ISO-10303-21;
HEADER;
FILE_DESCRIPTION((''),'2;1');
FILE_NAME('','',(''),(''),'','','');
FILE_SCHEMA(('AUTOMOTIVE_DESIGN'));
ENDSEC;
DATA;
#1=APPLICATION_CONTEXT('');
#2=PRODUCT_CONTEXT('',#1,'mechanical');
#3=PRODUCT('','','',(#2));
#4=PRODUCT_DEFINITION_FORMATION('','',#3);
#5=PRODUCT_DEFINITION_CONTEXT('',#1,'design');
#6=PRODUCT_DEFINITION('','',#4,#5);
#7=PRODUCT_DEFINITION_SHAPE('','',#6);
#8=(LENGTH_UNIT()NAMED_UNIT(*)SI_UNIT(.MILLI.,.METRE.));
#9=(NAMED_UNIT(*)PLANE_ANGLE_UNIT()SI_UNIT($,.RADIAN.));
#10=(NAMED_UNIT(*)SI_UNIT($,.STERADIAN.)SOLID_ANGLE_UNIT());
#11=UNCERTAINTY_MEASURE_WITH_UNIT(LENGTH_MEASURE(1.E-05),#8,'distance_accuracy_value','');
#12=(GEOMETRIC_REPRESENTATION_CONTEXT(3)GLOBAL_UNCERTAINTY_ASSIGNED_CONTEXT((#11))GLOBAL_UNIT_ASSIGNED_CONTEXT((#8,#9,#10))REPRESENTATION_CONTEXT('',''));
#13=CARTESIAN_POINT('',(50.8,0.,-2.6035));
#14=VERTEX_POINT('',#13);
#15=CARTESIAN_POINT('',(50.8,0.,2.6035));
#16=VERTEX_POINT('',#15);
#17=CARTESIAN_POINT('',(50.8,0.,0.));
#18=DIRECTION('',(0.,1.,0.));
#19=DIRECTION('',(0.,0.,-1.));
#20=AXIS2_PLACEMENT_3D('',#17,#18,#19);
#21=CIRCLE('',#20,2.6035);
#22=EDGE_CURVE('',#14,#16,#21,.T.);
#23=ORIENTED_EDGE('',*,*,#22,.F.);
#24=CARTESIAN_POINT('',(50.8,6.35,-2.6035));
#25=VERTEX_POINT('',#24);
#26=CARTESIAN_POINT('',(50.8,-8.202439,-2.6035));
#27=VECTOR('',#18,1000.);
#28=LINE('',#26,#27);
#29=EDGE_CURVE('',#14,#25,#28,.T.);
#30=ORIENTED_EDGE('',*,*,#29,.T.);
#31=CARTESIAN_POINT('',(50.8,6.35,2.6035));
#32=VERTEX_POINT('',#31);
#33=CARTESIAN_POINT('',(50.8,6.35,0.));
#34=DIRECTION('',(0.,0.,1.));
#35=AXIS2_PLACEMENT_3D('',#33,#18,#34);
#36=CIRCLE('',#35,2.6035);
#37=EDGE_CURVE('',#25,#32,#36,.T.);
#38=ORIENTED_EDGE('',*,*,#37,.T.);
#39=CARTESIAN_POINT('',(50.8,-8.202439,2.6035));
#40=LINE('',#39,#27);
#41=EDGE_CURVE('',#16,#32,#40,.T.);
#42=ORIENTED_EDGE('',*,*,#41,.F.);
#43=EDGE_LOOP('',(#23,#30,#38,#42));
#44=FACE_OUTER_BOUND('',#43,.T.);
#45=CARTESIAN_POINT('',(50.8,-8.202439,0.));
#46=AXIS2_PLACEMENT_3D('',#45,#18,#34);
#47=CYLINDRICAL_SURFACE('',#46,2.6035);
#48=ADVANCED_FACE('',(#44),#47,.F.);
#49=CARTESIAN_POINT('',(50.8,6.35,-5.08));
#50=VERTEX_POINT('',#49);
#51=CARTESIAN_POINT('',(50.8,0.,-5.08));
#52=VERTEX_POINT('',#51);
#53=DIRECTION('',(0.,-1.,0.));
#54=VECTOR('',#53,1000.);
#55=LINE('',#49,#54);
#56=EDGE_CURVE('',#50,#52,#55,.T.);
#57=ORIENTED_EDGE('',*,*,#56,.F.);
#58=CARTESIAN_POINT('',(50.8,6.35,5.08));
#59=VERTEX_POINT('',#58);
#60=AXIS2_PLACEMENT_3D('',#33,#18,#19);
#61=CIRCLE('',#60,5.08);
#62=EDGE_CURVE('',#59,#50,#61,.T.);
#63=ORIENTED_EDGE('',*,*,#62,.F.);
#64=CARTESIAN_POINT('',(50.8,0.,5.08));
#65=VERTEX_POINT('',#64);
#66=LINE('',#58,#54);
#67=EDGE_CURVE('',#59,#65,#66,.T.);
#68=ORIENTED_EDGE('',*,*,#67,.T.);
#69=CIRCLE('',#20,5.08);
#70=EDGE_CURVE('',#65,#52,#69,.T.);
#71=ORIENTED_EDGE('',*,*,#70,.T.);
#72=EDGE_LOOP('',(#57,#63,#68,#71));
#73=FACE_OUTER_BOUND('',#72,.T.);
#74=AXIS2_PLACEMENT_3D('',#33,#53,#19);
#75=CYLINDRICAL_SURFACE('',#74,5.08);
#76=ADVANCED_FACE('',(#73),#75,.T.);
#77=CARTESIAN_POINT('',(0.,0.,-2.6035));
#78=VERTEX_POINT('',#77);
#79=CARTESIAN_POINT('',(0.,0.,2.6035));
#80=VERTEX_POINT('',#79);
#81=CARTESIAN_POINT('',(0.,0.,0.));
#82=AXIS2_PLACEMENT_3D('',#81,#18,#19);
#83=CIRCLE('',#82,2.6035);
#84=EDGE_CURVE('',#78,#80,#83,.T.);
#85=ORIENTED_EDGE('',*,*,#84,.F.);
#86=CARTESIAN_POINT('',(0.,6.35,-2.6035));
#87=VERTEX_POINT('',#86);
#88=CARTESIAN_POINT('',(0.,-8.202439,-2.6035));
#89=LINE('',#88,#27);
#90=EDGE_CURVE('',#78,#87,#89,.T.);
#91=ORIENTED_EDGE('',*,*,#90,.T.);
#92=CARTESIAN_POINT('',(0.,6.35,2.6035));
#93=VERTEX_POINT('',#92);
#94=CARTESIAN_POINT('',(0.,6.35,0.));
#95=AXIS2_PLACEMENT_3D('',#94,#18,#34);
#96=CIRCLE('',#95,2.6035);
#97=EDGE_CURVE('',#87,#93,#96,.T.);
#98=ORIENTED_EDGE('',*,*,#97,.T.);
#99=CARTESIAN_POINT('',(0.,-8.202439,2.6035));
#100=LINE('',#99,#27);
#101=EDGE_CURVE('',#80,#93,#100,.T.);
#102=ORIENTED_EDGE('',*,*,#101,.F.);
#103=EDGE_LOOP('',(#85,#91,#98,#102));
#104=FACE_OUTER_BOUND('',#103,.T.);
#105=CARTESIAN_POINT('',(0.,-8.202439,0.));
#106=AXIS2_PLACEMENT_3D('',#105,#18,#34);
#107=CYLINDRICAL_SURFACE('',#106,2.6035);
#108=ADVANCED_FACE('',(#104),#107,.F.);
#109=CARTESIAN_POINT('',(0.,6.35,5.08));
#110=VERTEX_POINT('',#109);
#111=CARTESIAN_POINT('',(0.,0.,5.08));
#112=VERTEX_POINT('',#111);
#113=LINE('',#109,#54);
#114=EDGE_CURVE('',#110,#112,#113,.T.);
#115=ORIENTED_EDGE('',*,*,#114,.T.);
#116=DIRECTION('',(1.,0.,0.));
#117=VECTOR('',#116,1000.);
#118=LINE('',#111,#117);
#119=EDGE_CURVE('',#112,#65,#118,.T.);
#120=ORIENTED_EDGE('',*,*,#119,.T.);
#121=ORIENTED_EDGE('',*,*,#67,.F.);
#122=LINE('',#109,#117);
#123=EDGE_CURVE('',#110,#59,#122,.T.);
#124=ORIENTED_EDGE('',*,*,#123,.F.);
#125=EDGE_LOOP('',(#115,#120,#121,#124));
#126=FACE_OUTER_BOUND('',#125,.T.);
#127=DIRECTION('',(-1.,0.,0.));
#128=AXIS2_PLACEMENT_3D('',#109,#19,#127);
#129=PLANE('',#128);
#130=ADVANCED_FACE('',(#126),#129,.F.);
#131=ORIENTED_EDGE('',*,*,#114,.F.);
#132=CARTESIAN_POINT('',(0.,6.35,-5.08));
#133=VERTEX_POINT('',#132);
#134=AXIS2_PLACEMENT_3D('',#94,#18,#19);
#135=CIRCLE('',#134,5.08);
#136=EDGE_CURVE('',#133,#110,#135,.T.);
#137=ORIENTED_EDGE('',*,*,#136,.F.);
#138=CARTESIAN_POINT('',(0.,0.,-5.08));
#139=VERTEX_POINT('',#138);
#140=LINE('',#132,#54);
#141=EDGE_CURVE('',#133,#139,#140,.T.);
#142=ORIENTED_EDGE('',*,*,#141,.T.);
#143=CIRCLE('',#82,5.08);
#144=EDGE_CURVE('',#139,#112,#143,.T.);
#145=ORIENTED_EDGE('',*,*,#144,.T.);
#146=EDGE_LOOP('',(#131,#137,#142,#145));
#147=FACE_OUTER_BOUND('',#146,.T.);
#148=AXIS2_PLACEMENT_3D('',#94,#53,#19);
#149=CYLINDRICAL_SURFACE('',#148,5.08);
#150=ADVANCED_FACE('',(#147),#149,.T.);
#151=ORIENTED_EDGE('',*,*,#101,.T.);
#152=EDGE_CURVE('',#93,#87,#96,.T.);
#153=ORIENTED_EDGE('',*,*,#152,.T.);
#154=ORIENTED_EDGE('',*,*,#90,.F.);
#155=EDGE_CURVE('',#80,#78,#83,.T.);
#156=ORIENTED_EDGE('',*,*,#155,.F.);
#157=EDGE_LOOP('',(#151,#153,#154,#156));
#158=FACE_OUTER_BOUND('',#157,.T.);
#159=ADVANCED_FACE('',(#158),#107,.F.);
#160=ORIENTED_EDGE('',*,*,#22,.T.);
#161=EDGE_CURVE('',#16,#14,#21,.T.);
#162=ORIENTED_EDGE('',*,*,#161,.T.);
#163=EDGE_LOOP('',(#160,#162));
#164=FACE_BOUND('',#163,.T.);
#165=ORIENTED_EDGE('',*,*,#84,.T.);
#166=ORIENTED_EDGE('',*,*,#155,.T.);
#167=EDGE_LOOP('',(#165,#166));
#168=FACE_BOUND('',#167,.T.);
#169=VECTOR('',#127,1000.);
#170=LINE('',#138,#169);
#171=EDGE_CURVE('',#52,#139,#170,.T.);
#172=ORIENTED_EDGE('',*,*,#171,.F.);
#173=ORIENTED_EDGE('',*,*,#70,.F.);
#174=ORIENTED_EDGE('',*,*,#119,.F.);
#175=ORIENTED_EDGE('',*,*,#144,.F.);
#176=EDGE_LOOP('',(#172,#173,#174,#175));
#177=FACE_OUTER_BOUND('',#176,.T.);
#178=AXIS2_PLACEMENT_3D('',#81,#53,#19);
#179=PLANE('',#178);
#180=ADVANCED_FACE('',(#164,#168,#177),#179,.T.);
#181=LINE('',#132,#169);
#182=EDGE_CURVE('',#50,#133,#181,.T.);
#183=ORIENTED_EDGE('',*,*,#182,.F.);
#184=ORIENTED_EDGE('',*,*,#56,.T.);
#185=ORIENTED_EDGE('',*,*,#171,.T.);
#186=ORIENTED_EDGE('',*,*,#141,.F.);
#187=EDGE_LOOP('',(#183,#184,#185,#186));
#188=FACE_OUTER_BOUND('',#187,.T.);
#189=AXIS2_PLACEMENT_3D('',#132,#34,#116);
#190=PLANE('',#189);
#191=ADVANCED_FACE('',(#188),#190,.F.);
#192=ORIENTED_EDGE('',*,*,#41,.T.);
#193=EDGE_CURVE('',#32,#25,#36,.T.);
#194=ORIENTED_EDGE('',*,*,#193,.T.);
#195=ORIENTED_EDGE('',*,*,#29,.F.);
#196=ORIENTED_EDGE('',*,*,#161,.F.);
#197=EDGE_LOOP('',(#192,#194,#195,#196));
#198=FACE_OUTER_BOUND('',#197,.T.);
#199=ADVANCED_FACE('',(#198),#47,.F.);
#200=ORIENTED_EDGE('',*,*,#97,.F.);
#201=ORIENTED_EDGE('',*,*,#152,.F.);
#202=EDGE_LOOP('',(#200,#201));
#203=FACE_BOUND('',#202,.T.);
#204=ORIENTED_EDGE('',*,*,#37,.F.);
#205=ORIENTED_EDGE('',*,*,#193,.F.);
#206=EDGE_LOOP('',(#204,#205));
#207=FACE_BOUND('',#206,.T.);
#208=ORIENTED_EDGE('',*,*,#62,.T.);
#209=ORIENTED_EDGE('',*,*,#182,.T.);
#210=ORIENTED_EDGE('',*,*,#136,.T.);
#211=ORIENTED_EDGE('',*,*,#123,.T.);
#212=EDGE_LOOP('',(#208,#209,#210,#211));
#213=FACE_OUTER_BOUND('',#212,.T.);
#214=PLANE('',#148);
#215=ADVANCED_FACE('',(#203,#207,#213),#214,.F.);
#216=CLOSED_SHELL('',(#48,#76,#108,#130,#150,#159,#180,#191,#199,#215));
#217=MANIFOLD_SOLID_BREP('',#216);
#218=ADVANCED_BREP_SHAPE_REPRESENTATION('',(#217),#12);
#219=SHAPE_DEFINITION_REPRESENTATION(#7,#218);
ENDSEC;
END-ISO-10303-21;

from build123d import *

# Parameters (mm, degrees)
SKETCH1_R           = 2.9
BOSS_EXTRUDE1_DEPTH = 6.35
BOSS_EXTRUDE2_START = -6.35
SKETCH2_R           = 2.9
SKETCH2_R_2         = 2.6035
BOSS_EXTRUDE2_DEPTH = 6.35


with BuildPart() as part:
    # Sketch1 → Boss-Extrude1 (new body)
    with BuildSketch(Plane(origin=(0, 0, 0), x_dir=(1, 0, 0), z_dir=(0, 1, 0))):
        with BuildLine():
            Line((0, 5.08), (50.8, 5.08))
            ThreePointArc((50.8, 5.08), (55.88, 0), (50.8, -5.08))
            Line((50.8, -5.08), (0, -5.08))
            ThreePointArc((0, -5.08), (-5.08, 0), (0, 5.08))
        make_face()
        with Locations(Location((0, 0, 0), (0, 0, 270))):
            Circle(SKETCH1_R, mode=Mode.SUBTRACT)
        with Locations(Location((50.8, 0, 0), (0, 0, 270))):
            Circle(SKETCH1_R, mode=Mode.SUBTRACT)
    extrude(amount=BOSS_EXTRUDE1_DEPTH)

    # Sketch2 → Boss-Extrude2 (add)
    # profile 1 of 2: a face of its own
    with BuildSketch(Plane(origin=(0, 6.35, 0), x_dir=(1, 0, 0), z_dir=(0, 1, 0)).offset(BOSS_EXTRUDE2_START)):
        Circle(SKETCH2_R)
        with Locations(Location((0, 0, 0), (0, 0, 270))):
            Circle(SKETCH2_R_2, mode=Mode.SUBTRACT)
    # profile 2 of 2: a face of its own
    with BuildSketch(Plane(origin=(0, 6.35, 0), x_dir=(1, 0, 0), z_dir=(0, 1, 0)).offset(BOSS_EXTRUDE2_START)):
        with Locations((50.8, 0)):
            Circle(SKETCH2_R)
        with Locations(Location((50.8, 0, 0), (0, 0, 270))):
            Circle(SKETCH2_R_2, mode=Mode.SUBTRACT)
    extrude(amount=BOSS_EXTRUDE2_DEPTH)


solid = part.part
